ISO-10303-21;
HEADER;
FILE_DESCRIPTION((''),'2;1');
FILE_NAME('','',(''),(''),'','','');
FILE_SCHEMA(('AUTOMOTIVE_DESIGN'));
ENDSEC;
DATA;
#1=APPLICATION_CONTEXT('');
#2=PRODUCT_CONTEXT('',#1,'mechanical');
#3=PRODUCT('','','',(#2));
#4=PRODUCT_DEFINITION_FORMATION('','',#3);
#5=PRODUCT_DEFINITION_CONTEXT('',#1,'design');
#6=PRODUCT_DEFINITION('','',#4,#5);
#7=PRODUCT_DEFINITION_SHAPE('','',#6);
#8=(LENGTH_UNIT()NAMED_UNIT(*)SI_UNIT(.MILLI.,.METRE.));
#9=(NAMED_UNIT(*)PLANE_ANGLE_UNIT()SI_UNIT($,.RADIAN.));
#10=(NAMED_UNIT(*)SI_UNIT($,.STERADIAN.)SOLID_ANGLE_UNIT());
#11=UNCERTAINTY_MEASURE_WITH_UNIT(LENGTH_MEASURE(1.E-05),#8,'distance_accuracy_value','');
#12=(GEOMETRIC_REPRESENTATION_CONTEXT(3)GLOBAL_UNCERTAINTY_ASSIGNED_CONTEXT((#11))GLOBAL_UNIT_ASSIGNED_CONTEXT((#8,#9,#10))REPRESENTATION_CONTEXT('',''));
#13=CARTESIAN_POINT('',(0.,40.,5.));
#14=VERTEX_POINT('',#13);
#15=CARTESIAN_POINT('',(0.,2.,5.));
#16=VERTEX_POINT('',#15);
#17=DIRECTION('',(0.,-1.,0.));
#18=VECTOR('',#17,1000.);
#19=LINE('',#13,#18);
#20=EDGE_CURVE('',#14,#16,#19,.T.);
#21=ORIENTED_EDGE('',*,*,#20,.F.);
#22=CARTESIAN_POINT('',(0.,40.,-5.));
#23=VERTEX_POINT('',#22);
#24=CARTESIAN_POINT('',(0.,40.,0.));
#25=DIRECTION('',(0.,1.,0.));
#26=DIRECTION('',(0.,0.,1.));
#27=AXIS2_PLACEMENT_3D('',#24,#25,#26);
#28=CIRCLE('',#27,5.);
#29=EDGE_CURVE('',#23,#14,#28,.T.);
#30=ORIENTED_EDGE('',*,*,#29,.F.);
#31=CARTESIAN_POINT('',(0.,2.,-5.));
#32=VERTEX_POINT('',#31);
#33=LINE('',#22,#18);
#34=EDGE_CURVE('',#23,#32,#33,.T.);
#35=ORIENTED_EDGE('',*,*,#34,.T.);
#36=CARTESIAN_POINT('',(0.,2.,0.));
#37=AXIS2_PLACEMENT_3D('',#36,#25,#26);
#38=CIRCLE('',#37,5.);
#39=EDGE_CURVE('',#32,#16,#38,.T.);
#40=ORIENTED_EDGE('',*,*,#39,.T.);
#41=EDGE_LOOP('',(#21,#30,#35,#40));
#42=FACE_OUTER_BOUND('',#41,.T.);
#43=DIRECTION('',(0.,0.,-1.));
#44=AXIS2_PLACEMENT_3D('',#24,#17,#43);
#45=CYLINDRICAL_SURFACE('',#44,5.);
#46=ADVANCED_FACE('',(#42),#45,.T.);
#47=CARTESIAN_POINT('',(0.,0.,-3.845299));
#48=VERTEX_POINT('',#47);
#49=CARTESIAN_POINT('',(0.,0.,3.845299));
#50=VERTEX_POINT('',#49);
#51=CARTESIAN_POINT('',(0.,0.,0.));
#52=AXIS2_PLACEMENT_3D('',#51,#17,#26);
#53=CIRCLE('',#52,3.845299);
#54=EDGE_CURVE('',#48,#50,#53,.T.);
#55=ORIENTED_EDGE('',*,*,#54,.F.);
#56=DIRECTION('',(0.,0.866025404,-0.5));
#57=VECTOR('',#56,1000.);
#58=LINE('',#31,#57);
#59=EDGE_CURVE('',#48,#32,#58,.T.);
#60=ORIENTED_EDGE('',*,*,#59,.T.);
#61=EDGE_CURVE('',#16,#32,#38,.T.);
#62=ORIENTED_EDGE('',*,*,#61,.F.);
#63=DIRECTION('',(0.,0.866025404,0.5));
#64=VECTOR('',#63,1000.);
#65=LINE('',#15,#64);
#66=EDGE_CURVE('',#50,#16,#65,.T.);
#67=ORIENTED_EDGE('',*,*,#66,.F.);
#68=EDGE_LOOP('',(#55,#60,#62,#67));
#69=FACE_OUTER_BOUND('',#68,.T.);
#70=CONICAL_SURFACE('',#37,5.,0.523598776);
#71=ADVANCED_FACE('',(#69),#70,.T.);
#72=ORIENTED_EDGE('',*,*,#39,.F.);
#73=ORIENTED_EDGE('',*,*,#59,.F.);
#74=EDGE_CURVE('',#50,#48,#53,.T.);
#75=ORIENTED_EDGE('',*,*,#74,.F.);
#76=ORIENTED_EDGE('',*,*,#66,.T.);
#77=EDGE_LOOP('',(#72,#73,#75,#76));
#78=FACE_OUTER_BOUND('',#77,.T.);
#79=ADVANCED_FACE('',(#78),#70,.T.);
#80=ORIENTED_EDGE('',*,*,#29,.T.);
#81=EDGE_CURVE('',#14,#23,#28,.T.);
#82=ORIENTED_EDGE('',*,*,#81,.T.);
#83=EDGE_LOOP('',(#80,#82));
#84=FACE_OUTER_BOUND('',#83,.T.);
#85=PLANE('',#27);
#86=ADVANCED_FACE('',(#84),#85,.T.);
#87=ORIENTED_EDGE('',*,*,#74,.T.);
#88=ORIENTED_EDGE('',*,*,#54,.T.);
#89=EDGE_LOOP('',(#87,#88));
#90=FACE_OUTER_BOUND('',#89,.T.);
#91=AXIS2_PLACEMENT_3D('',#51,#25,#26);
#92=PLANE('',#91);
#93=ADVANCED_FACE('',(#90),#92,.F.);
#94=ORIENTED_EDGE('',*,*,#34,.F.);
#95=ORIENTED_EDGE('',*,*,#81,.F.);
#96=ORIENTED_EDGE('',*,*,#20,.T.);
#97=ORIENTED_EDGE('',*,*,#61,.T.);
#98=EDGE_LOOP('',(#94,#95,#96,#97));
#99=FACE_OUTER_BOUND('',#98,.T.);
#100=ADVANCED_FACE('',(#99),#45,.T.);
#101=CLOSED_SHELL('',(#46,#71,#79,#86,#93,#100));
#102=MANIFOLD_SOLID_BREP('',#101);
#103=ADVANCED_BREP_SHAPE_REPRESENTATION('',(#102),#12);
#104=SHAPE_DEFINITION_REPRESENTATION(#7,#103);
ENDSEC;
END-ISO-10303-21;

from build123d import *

# Parameters (mm, degrees)
SKETCH1_R           = 5
BOSS_EXTRUDE1_DEPTH = 40
CHAMFER1_SIZE       = 1.154700538
CHAMFER1_SIZE2      = 2


with BuildPart() as part:
    # Sketch1 → Boss-Extrude1 (new body)
    with BuildSketch(Plane(origin=(0, 0, 0), x_dir=(1, 0, 0), z_dir=(0, 1, 0))):
        with Locations(Location((0, 0, 0), (0, 0, 270))):
            Circle(SKETCH1_R)
    extrude(amount=BOSS_EXTRUDE1_DEPTH)

    # Chamfer1
    chamfer1_edges = [part.edges().sort_by_distance(p)[0] for p in [
        (0, 0, -5),
    ]]
    chamfer1_side = [part.faces().sort_by_distance(p)[0] for p in [
        (0, 0, 0),
    ]]
    chamfer(chamfer1_edges, length=CHAMFER1_SIZE, length2=CHAMFER1_SIZE2, reference=chamfer1_side[0])


solid = part.part
